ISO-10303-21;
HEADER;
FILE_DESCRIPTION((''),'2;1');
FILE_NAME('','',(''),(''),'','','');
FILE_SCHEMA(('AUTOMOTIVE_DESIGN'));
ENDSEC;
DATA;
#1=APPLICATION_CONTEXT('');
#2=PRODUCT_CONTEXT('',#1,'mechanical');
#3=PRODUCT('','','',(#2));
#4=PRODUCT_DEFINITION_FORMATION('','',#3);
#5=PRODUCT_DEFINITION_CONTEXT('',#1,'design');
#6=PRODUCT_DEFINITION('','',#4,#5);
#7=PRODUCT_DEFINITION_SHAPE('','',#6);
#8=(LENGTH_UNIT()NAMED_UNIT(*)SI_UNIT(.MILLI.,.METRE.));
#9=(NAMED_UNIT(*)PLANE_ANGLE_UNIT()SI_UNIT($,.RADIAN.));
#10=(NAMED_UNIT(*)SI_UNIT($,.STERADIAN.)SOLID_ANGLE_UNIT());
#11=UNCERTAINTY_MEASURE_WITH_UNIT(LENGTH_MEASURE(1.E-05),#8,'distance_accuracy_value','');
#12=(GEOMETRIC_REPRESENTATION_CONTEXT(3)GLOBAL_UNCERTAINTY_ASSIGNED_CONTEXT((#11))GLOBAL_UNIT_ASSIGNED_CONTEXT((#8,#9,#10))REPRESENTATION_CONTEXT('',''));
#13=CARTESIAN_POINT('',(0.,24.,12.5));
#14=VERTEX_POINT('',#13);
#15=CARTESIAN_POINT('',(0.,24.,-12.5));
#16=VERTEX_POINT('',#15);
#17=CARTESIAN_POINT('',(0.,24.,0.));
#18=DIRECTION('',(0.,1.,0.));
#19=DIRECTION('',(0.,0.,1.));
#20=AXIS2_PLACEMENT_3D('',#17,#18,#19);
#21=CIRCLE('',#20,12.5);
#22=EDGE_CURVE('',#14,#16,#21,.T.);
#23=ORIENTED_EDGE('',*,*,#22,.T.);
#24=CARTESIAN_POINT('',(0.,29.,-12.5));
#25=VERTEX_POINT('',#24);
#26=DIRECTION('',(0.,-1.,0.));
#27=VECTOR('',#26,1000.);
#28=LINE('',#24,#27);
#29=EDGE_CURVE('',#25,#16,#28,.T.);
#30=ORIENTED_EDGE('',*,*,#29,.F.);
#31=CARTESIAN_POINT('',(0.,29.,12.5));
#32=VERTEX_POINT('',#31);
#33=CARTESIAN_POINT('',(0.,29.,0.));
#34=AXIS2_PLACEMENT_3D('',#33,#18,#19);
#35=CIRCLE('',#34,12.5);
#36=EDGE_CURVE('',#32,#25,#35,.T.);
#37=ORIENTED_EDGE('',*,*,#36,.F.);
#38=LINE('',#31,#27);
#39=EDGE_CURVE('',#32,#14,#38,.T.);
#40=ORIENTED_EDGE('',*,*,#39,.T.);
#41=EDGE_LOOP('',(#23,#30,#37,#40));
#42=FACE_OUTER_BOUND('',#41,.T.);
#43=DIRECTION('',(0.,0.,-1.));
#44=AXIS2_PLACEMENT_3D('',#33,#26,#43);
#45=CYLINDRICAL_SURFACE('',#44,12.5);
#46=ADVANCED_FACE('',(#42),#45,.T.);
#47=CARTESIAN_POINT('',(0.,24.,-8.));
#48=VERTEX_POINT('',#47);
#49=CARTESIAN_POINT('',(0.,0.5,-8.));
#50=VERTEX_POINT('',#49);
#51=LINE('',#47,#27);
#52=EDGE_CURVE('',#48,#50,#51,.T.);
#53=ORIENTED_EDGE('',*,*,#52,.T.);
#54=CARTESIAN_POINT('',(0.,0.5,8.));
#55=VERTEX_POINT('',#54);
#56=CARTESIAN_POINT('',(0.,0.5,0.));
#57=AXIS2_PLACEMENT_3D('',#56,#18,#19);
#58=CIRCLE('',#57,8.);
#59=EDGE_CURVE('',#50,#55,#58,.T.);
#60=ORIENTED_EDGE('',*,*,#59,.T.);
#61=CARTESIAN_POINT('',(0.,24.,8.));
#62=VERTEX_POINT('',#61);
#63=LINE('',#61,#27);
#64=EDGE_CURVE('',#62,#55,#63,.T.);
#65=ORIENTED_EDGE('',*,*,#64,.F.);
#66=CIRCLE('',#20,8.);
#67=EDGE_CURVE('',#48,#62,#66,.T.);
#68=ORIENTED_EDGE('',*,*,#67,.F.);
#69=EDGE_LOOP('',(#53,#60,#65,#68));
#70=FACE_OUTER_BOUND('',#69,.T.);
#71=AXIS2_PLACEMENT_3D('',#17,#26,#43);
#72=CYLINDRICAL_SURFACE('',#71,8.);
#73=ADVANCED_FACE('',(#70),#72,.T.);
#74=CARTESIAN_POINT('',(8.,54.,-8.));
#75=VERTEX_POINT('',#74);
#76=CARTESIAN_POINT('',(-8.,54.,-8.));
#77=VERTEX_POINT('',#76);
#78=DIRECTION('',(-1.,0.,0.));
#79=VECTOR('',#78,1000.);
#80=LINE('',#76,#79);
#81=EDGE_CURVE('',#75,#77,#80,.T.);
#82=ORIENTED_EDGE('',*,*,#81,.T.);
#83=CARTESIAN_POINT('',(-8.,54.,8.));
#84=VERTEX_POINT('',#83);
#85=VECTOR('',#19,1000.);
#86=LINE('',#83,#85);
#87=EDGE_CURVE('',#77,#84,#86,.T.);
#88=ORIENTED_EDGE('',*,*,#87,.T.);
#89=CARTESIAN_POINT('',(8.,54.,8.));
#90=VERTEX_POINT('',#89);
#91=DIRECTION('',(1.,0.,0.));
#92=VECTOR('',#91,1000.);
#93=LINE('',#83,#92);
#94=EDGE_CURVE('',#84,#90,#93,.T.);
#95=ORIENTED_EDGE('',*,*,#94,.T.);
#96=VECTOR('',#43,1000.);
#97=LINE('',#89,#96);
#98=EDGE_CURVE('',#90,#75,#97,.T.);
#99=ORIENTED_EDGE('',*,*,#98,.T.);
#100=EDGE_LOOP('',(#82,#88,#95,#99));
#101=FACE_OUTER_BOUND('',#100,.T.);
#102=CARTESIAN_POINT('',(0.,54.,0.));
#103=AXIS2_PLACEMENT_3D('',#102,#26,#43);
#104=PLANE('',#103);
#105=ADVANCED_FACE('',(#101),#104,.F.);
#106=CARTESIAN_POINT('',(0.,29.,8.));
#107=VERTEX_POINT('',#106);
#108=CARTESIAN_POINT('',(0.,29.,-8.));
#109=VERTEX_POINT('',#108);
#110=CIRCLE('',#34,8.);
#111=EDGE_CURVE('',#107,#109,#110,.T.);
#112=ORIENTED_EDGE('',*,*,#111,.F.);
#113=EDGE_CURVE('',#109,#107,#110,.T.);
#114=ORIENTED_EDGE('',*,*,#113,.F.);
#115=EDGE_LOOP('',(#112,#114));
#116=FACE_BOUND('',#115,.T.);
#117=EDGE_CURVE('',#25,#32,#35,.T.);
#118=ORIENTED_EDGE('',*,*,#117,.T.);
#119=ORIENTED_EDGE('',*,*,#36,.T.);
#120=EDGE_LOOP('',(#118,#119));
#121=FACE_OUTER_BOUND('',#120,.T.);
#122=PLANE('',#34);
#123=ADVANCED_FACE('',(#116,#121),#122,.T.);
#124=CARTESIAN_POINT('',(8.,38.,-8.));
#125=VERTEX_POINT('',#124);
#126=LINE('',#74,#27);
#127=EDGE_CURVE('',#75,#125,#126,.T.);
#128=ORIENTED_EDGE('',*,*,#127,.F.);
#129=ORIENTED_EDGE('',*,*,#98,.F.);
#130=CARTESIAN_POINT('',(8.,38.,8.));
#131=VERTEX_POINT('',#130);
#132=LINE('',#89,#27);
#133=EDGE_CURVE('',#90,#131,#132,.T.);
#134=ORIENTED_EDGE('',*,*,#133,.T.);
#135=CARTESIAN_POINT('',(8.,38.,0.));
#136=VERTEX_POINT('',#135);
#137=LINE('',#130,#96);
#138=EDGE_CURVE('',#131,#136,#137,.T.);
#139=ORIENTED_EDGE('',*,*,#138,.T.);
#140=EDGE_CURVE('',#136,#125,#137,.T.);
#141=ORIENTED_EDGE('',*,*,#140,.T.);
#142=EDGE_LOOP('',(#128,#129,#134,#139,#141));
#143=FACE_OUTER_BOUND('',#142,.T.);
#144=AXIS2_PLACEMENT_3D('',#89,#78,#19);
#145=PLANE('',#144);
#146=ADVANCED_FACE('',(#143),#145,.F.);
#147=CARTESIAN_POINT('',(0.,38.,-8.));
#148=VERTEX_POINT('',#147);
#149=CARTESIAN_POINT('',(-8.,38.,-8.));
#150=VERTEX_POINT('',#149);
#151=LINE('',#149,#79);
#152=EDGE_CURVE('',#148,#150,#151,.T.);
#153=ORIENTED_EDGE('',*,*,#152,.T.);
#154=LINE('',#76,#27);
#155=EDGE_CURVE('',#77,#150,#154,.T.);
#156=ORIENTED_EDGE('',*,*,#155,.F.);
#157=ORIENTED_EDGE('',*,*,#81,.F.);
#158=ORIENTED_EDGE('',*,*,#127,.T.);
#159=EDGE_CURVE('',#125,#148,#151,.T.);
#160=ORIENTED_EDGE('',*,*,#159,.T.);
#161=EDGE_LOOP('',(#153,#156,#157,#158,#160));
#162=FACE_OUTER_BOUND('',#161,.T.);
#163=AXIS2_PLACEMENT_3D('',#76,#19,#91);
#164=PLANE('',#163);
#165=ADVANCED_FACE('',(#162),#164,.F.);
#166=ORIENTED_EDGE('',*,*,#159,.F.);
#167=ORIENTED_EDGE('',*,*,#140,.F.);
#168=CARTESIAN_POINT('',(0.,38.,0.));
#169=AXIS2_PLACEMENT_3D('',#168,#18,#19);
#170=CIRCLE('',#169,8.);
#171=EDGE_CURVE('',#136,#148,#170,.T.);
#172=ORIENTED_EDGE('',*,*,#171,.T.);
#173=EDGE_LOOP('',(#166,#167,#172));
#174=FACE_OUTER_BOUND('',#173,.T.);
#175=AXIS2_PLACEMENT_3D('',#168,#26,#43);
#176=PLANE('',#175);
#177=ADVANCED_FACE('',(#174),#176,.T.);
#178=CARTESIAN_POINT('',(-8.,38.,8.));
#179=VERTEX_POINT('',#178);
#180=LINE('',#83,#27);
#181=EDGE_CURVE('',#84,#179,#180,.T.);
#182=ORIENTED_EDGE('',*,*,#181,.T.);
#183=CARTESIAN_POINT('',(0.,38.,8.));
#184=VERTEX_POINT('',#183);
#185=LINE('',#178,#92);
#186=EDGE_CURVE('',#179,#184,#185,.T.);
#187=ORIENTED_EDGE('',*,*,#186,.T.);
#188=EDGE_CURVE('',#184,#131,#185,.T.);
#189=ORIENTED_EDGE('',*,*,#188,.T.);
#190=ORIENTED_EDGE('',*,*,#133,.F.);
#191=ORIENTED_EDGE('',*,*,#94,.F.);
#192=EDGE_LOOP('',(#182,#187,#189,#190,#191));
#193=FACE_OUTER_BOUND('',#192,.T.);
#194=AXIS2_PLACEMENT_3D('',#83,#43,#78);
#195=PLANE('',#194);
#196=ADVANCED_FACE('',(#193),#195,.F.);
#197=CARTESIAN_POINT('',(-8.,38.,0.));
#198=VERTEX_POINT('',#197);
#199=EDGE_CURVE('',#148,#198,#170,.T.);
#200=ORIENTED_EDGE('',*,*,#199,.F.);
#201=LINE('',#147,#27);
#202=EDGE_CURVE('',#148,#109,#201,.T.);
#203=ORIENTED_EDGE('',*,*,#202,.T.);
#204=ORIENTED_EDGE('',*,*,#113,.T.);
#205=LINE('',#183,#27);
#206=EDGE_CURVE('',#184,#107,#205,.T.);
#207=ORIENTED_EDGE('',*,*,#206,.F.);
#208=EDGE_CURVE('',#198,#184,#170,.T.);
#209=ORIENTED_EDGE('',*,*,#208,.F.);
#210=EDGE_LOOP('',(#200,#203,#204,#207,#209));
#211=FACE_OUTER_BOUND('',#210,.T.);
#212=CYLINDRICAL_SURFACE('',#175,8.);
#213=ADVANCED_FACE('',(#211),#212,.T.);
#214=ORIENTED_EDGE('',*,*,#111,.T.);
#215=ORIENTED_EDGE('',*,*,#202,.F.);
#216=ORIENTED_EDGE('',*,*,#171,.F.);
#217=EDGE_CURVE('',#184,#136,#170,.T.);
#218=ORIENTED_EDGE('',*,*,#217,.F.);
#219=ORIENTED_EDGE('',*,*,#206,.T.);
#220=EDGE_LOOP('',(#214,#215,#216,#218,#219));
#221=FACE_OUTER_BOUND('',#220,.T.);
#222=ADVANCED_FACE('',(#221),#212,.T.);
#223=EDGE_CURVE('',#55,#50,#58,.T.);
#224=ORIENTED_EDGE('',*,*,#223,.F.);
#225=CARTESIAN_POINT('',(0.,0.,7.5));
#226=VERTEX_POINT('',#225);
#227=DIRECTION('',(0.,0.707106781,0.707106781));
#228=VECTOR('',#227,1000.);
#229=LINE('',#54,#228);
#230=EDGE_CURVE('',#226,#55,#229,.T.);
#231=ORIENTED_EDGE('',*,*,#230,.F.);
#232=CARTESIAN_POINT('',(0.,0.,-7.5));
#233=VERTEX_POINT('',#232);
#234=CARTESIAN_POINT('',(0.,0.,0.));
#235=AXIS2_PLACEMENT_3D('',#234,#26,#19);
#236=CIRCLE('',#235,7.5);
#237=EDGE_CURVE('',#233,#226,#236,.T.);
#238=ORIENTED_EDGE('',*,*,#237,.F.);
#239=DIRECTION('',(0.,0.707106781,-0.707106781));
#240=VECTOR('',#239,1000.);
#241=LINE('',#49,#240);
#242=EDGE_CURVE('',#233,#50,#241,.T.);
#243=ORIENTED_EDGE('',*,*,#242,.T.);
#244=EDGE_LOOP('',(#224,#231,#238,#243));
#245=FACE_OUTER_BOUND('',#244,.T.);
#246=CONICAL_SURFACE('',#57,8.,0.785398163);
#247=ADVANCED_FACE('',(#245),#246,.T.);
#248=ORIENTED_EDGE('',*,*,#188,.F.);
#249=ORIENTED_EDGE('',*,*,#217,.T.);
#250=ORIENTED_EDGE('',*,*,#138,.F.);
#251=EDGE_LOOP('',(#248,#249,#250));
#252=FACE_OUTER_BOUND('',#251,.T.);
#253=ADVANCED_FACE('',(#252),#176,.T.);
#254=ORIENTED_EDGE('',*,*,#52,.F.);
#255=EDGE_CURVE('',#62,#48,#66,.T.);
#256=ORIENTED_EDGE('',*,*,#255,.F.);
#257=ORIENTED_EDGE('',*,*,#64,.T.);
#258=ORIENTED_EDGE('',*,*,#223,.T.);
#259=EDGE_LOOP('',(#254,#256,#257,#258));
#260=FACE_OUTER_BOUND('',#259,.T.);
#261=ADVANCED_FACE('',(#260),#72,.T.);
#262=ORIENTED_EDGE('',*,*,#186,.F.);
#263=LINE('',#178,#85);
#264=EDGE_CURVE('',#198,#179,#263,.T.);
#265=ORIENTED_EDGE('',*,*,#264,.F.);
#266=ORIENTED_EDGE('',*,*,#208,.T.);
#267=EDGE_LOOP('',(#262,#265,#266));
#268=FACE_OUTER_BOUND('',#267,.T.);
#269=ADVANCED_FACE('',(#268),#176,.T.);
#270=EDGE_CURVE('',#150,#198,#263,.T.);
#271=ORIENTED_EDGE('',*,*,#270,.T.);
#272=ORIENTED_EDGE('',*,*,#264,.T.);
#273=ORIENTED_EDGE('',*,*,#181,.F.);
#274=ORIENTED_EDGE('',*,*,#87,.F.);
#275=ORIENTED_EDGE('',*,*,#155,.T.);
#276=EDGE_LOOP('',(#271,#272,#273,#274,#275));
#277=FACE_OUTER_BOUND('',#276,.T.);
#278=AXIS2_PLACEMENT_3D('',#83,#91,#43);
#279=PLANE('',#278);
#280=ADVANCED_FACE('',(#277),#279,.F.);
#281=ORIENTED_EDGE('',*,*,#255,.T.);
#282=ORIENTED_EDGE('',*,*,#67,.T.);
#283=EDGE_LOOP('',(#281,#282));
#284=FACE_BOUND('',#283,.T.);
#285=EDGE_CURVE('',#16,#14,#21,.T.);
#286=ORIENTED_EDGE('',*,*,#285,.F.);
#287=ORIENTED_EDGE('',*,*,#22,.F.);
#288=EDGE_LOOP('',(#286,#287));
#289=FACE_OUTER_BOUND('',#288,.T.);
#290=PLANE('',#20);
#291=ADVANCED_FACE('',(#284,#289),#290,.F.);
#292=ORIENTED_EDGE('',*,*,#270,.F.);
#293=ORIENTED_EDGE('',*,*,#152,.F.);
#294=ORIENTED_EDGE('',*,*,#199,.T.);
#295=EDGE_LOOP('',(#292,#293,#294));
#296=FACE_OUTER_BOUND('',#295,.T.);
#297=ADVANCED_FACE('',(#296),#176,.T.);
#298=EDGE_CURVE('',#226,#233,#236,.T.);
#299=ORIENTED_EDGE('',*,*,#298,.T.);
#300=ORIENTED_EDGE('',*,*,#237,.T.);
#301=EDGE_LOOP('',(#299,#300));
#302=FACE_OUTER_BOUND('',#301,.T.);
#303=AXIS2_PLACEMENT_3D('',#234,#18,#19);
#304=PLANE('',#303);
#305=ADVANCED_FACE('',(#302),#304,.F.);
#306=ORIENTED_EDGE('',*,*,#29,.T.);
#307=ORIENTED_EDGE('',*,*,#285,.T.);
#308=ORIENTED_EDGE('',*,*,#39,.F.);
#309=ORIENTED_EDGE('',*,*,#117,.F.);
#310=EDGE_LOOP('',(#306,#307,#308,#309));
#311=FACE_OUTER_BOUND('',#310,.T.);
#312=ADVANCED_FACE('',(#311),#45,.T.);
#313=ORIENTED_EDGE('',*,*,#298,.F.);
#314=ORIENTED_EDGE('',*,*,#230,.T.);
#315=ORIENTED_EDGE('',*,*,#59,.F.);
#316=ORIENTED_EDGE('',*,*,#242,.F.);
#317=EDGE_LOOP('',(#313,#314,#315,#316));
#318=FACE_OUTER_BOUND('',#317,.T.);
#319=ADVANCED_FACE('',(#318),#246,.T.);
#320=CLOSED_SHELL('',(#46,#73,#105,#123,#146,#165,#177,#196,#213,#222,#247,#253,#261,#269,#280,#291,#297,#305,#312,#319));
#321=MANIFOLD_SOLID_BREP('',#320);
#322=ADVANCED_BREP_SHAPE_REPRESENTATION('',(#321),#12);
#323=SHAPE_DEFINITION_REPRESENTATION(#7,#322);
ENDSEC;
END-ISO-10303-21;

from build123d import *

# Parameters (mm, degrees)
SHANK_SKETCH_16_R             = 8
SHANK_16X24_DEPTH             = 24
SHANK_END_CHAMFER_0_5X45_SIZE = 0.5
COLLAR_SKETCH_25_R            = 12.5
COLLAR_25X5_DEPTH             = 5
NECK_SKETCH_16_R              = 8
NECK_16X9_DEPTH               = 9
SQUARE_HEAD_SKETCH_16X16_W    = 16
SQUARE_HEAD_SKETCH_16X16_H    = 16
SQUARE_HEAD_16X16X16_DEPTH    = 16


with BuildPart() as part:
    # Shank Sketch Ø16 → Shank Ø16x24 (new body)
    with BuildSketch(Plane(origin=(0, 0, 0), x_dir=(1, 0, 0), z_dir=(0, 1, 0))):
        with Locations(Location((0, 0, 0), (0, 0, 270))):
            Circle(SHANK_SKETCH_16_R)
    extrude(amount=SHANK_16X24_DEPTH)

    # Shank End Chamfer 0.5x45
    shank_end_chamfer_0_5x45_edges = [part.edges().sort_by_distance(p)[0] for p in [
        (0, 0, -8),
    ]]
    chamfer(shank_end_chamfer_0_5x45_edges, length=SHANK_END_CHAMFER_0_5X45_SIZE)

    # Collar Sketch Ø25 → Collar Ø25x5 (add)
    with BuildSketch(Plane(origin=(0, 24, 0), x_dir=(1, 0, 0), z_dir=(0, 1, 0))):
        with Locations(Location((0, 0, 0), (0, 0, 270))):
            Circle(COLLAR_SKETCH_25_R)
    extrude(amount=COLLAR_25X5_DEPTH)

    # Neck Sketch Ø16 → Neck Ø16x9 (add)
    with BuildSketch(Plane(origin=(0, 29, 0), x_dir=(1, 0, 0), z_dir=(0, 1, 0))):
        with Locations(Location((0, 0, 0), (0, 0, 270))):
            Circle(NECK_SKETCH_16_R)
    extrude(amount=NECK_16X9_DEPTH)

    # Square Head Sketch 16x16 → Square Head 16x16x16 (add)
    with BuildSketch(Plane(origin=(0, 38, 0), x_dir=(1, 0, 0), z_dir=(0, 1, 0))):
        Rectangle(SQUARE_HEAD_SKETCH_16X16_W, SQUARE_HEAD_SKETCH_16X16_H)
    extrude(amount=SQUARE_HEAD_16X16X16_DEPTH)


solid = part.part
